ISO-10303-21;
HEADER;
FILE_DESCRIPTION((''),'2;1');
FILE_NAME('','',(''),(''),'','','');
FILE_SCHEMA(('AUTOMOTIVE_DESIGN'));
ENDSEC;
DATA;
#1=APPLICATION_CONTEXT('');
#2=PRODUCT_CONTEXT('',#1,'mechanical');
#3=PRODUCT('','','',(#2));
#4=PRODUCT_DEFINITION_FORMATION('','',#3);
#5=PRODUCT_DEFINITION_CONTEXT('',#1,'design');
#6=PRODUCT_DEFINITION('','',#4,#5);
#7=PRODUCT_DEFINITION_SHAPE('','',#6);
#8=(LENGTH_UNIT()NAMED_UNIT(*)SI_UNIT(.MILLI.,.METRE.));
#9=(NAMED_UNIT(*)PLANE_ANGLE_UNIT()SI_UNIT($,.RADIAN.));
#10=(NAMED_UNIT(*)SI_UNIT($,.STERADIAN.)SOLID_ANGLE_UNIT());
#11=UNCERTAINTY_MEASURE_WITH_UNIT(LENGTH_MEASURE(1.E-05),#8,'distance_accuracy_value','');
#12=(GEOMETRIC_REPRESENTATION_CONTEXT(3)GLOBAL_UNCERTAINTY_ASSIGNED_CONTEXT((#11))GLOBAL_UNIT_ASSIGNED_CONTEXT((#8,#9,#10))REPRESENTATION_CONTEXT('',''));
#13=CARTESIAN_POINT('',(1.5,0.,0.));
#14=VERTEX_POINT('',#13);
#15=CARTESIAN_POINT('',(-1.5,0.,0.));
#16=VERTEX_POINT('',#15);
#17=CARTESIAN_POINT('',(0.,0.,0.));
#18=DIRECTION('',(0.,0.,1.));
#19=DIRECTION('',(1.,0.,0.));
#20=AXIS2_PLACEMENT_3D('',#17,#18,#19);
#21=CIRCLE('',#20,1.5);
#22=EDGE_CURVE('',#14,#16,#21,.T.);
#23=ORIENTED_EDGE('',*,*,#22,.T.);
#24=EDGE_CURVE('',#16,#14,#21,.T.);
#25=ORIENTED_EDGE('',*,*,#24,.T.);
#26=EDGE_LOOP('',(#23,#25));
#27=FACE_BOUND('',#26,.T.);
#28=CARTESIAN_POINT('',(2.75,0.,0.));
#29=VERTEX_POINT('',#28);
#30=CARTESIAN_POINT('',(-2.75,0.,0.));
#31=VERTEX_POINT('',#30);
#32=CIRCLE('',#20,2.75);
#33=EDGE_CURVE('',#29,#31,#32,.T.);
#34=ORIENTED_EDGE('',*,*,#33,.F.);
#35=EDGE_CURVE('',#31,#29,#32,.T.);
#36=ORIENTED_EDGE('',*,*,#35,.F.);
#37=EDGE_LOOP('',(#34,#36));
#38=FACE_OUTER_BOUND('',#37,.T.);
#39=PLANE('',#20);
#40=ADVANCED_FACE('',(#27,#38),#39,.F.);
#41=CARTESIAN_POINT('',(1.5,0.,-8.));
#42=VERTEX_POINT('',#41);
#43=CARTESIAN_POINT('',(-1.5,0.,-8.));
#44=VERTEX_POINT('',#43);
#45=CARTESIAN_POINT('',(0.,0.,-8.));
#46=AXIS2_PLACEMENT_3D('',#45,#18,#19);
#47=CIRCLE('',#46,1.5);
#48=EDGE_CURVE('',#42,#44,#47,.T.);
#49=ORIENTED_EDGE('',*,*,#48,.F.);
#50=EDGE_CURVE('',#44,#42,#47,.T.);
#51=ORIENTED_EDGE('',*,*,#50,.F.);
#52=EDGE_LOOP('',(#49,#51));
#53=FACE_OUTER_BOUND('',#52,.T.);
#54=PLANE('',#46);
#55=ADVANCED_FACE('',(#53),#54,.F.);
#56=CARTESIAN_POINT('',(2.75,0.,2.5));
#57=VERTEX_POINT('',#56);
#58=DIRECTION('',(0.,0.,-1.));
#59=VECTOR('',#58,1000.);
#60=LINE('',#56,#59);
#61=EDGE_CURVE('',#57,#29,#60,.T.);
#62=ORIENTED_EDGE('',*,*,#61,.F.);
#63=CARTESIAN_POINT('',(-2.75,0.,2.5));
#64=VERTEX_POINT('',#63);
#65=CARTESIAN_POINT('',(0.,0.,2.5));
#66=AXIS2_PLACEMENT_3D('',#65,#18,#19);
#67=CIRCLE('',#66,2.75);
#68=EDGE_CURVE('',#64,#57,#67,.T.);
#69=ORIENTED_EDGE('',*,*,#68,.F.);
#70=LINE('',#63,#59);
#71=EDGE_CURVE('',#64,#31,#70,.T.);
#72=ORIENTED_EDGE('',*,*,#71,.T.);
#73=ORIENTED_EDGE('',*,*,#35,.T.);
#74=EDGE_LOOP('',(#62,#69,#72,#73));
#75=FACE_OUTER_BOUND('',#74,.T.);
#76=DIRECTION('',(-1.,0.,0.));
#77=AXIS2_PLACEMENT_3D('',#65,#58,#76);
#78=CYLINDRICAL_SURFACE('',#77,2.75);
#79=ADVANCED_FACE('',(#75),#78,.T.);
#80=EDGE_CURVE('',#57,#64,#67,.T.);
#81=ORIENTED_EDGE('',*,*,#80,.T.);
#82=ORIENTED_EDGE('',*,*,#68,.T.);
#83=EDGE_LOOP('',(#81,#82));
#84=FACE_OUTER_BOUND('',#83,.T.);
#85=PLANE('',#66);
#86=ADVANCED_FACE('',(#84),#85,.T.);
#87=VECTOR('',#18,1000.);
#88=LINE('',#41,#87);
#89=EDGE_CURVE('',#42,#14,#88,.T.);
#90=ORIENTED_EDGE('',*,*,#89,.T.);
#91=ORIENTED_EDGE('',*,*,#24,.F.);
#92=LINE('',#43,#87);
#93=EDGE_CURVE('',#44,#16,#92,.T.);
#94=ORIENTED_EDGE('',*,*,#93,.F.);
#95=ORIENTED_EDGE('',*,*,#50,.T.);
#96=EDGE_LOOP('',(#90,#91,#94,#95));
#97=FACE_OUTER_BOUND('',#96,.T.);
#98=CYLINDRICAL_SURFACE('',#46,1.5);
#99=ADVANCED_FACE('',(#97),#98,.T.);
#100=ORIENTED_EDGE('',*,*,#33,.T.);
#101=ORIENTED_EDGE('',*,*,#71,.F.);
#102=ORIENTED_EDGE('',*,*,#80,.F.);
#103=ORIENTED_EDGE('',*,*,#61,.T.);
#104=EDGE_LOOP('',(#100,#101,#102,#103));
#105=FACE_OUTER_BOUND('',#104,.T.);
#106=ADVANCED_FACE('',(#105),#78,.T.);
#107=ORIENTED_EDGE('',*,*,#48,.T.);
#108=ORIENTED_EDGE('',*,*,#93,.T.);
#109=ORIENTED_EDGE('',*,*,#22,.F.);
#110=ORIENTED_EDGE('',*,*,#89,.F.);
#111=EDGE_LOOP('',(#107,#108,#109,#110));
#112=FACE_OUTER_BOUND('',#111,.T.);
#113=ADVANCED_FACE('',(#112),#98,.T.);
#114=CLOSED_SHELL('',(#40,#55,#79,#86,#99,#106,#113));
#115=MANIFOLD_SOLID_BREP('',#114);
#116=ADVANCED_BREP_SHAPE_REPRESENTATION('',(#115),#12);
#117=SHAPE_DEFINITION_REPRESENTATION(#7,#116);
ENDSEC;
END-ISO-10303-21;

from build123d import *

# Parameters (mm, degrees)
SKETCH_1_R      = 1.5
EXTRUDE_1_DEPTH = 8
SKETCH_2_R      = 2.75
EXTRUDE_2_DEPTH = 2.5


with BuildPart() as part:
    # 草图1 → 凸台-拉伸1 (new body)
    with BuildSketch(Plane.XY):
        Circle(SKETCH_1_R)
    extrude(amount=-EXTRUDE_1_DEPTH)

    # 草图2 → 凸台-拉伸2 (add)
    with BuildSketch(Plane.XY):
        Circle(SKETCH_2_R)
    extrude(amount=EXTRUDE_2_DEPTH)


solid = part.part
